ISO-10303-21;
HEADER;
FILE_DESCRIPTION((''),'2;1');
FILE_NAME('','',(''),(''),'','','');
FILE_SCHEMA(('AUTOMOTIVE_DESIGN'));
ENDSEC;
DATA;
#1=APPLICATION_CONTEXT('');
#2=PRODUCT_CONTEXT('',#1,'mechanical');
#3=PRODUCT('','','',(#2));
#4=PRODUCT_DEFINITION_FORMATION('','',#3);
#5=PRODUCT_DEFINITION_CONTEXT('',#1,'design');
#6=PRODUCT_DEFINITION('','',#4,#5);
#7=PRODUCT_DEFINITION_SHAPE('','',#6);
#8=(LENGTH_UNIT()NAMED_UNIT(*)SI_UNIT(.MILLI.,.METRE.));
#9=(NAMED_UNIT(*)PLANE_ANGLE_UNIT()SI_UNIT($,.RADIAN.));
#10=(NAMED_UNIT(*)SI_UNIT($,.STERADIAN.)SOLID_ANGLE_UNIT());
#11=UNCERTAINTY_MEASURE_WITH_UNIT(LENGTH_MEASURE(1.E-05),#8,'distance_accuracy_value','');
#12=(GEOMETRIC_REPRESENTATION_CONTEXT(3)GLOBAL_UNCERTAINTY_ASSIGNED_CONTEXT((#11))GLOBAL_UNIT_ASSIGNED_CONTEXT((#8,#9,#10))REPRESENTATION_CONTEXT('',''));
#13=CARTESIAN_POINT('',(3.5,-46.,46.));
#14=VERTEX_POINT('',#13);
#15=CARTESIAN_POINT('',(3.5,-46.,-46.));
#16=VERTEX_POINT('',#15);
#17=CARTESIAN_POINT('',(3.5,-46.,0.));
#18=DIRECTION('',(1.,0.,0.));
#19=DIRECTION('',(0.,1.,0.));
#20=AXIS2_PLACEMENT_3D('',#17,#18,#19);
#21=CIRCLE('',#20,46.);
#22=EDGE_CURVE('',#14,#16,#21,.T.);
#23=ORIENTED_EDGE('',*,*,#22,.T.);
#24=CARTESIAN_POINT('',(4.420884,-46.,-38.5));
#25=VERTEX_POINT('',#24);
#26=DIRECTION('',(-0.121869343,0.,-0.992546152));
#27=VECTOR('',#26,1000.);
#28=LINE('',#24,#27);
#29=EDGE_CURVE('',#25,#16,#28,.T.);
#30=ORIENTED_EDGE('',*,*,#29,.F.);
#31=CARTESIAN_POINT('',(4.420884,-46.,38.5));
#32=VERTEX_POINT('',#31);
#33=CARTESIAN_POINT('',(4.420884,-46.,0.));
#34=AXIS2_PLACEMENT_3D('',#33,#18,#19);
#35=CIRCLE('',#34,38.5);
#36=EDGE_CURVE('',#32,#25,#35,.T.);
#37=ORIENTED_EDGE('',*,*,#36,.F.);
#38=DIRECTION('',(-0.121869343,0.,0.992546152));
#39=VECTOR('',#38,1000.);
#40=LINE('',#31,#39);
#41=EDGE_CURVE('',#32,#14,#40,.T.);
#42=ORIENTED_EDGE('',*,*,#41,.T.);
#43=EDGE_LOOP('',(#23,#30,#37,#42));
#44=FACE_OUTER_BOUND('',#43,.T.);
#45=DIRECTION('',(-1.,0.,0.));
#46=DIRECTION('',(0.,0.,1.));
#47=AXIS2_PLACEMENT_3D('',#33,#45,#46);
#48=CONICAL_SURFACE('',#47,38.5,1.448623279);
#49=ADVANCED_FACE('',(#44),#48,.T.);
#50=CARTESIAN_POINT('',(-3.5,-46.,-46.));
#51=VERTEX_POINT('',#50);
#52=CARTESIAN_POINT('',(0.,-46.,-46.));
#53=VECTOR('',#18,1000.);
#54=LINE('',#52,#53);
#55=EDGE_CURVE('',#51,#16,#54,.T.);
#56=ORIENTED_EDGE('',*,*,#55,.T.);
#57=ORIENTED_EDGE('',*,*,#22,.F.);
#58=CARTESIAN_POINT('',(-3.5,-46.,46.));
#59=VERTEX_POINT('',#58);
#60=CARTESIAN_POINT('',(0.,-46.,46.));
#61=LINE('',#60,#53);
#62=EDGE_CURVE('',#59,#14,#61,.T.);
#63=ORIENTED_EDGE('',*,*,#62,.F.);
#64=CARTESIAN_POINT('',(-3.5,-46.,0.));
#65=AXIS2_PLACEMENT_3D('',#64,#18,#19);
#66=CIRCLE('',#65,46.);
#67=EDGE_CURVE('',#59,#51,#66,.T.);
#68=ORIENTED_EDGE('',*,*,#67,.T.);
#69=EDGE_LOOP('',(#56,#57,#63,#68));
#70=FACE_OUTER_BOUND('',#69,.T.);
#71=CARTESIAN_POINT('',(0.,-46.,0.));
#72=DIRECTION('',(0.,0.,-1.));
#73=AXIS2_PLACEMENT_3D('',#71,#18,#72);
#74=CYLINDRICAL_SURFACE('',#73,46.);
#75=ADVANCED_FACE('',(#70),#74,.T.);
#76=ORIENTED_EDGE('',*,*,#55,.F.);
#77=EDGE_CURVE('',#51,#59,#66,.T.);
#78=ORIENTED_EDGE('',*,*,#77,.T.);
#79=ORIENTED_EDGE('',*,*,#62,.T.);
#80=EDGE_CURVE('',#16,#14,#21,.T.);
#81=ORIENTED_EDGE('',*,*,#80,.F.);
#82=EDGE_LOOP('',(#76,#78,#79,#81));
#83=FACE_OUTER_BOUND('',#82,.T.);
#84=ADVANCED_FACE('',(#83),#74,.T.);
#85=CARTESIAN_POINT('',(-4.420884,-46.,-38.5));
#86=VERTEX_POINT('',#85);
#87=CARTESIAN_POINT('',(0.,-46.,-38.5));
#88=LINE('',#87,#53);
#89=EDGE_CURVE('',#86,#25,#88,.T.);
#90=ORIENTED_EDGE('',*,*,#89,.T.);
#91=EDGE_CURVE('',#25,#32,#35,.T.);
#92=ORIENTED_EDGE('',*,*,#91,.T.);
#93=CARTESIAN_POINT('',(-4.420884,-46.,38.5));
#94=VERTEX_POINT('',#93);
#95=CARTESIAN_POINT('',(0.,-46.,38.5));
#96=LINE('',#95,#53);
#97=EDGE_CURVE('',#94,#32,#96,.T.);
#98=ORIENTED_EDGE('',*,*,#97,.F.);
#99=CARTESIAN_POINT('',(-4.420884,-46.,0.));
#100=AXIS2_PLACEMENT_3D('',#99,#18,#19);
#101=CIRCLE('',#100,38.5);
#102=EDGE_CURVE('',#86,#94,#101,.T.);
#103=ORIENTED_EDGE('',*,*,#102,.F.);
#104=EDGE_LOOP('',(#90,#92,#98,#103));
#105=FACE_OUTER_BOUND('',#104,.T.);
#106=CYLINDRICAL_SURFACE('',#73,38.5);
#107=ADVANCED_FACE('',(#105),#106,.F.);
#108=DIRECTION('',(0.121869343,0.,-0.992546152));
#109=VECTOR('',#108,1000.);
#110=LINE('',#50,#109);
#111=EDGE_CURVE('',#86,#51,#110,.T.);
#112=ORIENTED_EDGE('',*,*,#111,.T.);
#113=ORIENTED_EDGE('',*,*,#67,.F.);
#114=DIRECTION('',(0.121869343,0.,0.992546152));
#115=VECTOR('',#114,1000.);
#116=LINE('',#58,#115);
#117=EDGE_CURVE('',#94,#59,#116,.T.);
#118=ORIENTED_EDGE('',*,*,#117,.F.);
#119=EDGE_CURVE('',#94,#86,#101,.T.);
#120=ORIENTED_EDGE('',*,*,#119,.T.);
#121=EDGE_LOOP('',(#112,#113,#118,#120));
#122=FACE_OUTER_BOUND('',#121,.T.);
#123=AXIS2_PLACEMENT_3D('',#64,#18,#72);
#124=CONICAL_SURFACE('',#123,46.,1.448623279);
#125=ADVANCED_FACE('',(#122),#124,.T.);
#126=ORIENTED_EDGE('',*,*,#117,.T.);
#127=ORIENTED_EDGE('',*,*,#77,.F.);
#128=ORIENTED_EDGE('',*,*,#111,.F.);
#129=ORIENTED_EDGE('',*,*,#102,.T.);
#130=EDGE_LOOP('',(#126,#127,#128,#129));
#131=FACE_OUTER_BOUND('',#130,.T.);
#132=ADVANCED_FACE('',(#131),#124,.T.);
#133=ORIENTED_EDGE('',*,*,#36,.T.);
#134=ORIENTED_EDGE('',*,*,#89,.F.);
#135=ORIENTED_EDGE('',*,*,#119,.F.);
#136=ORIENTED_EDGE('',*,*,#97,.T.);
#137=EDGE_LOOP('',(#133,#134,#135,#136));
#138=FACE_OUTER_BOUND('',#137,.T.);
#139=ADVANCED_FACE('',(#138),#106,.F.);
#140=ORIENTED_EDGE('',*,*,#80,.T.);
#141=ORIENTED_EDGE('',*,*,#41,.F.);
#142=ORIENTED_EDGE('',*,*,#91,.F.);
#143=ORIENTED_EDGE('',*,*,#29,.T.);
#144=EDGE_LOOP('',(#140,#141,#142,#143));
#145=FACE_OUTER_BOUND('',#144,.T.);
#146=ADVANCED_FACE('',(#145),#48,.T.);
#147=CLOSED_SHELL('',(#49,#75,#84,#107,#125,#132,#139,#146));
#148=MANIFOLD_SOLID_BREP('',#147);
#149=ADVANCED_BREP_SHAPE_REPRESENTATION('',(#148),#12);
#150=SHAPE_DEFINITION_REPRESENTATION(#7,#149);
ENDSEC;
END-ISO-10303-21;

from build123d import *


with BuildPart() as part:
    # Sweep1: sweep along a path in Sketch3
    with BuildLine(Plane(origin=(0, 0, 0), x_dir=(0, 0, -1), z_dir=(1, 0, 0))) as sweep1_path:
        CenterArc((0, -46), 46, 0, 360)
    # Sketch2 → Sweep1 (sweep)
    with BuildSketch(Plane.XY):
        Polygon((-3.5, 0), (3.5, 0), (4.420884207, -7.5), (-4.420884207, -7.5), align=None)
    sweep(path=sweep1_path.line)


solid = part.part
